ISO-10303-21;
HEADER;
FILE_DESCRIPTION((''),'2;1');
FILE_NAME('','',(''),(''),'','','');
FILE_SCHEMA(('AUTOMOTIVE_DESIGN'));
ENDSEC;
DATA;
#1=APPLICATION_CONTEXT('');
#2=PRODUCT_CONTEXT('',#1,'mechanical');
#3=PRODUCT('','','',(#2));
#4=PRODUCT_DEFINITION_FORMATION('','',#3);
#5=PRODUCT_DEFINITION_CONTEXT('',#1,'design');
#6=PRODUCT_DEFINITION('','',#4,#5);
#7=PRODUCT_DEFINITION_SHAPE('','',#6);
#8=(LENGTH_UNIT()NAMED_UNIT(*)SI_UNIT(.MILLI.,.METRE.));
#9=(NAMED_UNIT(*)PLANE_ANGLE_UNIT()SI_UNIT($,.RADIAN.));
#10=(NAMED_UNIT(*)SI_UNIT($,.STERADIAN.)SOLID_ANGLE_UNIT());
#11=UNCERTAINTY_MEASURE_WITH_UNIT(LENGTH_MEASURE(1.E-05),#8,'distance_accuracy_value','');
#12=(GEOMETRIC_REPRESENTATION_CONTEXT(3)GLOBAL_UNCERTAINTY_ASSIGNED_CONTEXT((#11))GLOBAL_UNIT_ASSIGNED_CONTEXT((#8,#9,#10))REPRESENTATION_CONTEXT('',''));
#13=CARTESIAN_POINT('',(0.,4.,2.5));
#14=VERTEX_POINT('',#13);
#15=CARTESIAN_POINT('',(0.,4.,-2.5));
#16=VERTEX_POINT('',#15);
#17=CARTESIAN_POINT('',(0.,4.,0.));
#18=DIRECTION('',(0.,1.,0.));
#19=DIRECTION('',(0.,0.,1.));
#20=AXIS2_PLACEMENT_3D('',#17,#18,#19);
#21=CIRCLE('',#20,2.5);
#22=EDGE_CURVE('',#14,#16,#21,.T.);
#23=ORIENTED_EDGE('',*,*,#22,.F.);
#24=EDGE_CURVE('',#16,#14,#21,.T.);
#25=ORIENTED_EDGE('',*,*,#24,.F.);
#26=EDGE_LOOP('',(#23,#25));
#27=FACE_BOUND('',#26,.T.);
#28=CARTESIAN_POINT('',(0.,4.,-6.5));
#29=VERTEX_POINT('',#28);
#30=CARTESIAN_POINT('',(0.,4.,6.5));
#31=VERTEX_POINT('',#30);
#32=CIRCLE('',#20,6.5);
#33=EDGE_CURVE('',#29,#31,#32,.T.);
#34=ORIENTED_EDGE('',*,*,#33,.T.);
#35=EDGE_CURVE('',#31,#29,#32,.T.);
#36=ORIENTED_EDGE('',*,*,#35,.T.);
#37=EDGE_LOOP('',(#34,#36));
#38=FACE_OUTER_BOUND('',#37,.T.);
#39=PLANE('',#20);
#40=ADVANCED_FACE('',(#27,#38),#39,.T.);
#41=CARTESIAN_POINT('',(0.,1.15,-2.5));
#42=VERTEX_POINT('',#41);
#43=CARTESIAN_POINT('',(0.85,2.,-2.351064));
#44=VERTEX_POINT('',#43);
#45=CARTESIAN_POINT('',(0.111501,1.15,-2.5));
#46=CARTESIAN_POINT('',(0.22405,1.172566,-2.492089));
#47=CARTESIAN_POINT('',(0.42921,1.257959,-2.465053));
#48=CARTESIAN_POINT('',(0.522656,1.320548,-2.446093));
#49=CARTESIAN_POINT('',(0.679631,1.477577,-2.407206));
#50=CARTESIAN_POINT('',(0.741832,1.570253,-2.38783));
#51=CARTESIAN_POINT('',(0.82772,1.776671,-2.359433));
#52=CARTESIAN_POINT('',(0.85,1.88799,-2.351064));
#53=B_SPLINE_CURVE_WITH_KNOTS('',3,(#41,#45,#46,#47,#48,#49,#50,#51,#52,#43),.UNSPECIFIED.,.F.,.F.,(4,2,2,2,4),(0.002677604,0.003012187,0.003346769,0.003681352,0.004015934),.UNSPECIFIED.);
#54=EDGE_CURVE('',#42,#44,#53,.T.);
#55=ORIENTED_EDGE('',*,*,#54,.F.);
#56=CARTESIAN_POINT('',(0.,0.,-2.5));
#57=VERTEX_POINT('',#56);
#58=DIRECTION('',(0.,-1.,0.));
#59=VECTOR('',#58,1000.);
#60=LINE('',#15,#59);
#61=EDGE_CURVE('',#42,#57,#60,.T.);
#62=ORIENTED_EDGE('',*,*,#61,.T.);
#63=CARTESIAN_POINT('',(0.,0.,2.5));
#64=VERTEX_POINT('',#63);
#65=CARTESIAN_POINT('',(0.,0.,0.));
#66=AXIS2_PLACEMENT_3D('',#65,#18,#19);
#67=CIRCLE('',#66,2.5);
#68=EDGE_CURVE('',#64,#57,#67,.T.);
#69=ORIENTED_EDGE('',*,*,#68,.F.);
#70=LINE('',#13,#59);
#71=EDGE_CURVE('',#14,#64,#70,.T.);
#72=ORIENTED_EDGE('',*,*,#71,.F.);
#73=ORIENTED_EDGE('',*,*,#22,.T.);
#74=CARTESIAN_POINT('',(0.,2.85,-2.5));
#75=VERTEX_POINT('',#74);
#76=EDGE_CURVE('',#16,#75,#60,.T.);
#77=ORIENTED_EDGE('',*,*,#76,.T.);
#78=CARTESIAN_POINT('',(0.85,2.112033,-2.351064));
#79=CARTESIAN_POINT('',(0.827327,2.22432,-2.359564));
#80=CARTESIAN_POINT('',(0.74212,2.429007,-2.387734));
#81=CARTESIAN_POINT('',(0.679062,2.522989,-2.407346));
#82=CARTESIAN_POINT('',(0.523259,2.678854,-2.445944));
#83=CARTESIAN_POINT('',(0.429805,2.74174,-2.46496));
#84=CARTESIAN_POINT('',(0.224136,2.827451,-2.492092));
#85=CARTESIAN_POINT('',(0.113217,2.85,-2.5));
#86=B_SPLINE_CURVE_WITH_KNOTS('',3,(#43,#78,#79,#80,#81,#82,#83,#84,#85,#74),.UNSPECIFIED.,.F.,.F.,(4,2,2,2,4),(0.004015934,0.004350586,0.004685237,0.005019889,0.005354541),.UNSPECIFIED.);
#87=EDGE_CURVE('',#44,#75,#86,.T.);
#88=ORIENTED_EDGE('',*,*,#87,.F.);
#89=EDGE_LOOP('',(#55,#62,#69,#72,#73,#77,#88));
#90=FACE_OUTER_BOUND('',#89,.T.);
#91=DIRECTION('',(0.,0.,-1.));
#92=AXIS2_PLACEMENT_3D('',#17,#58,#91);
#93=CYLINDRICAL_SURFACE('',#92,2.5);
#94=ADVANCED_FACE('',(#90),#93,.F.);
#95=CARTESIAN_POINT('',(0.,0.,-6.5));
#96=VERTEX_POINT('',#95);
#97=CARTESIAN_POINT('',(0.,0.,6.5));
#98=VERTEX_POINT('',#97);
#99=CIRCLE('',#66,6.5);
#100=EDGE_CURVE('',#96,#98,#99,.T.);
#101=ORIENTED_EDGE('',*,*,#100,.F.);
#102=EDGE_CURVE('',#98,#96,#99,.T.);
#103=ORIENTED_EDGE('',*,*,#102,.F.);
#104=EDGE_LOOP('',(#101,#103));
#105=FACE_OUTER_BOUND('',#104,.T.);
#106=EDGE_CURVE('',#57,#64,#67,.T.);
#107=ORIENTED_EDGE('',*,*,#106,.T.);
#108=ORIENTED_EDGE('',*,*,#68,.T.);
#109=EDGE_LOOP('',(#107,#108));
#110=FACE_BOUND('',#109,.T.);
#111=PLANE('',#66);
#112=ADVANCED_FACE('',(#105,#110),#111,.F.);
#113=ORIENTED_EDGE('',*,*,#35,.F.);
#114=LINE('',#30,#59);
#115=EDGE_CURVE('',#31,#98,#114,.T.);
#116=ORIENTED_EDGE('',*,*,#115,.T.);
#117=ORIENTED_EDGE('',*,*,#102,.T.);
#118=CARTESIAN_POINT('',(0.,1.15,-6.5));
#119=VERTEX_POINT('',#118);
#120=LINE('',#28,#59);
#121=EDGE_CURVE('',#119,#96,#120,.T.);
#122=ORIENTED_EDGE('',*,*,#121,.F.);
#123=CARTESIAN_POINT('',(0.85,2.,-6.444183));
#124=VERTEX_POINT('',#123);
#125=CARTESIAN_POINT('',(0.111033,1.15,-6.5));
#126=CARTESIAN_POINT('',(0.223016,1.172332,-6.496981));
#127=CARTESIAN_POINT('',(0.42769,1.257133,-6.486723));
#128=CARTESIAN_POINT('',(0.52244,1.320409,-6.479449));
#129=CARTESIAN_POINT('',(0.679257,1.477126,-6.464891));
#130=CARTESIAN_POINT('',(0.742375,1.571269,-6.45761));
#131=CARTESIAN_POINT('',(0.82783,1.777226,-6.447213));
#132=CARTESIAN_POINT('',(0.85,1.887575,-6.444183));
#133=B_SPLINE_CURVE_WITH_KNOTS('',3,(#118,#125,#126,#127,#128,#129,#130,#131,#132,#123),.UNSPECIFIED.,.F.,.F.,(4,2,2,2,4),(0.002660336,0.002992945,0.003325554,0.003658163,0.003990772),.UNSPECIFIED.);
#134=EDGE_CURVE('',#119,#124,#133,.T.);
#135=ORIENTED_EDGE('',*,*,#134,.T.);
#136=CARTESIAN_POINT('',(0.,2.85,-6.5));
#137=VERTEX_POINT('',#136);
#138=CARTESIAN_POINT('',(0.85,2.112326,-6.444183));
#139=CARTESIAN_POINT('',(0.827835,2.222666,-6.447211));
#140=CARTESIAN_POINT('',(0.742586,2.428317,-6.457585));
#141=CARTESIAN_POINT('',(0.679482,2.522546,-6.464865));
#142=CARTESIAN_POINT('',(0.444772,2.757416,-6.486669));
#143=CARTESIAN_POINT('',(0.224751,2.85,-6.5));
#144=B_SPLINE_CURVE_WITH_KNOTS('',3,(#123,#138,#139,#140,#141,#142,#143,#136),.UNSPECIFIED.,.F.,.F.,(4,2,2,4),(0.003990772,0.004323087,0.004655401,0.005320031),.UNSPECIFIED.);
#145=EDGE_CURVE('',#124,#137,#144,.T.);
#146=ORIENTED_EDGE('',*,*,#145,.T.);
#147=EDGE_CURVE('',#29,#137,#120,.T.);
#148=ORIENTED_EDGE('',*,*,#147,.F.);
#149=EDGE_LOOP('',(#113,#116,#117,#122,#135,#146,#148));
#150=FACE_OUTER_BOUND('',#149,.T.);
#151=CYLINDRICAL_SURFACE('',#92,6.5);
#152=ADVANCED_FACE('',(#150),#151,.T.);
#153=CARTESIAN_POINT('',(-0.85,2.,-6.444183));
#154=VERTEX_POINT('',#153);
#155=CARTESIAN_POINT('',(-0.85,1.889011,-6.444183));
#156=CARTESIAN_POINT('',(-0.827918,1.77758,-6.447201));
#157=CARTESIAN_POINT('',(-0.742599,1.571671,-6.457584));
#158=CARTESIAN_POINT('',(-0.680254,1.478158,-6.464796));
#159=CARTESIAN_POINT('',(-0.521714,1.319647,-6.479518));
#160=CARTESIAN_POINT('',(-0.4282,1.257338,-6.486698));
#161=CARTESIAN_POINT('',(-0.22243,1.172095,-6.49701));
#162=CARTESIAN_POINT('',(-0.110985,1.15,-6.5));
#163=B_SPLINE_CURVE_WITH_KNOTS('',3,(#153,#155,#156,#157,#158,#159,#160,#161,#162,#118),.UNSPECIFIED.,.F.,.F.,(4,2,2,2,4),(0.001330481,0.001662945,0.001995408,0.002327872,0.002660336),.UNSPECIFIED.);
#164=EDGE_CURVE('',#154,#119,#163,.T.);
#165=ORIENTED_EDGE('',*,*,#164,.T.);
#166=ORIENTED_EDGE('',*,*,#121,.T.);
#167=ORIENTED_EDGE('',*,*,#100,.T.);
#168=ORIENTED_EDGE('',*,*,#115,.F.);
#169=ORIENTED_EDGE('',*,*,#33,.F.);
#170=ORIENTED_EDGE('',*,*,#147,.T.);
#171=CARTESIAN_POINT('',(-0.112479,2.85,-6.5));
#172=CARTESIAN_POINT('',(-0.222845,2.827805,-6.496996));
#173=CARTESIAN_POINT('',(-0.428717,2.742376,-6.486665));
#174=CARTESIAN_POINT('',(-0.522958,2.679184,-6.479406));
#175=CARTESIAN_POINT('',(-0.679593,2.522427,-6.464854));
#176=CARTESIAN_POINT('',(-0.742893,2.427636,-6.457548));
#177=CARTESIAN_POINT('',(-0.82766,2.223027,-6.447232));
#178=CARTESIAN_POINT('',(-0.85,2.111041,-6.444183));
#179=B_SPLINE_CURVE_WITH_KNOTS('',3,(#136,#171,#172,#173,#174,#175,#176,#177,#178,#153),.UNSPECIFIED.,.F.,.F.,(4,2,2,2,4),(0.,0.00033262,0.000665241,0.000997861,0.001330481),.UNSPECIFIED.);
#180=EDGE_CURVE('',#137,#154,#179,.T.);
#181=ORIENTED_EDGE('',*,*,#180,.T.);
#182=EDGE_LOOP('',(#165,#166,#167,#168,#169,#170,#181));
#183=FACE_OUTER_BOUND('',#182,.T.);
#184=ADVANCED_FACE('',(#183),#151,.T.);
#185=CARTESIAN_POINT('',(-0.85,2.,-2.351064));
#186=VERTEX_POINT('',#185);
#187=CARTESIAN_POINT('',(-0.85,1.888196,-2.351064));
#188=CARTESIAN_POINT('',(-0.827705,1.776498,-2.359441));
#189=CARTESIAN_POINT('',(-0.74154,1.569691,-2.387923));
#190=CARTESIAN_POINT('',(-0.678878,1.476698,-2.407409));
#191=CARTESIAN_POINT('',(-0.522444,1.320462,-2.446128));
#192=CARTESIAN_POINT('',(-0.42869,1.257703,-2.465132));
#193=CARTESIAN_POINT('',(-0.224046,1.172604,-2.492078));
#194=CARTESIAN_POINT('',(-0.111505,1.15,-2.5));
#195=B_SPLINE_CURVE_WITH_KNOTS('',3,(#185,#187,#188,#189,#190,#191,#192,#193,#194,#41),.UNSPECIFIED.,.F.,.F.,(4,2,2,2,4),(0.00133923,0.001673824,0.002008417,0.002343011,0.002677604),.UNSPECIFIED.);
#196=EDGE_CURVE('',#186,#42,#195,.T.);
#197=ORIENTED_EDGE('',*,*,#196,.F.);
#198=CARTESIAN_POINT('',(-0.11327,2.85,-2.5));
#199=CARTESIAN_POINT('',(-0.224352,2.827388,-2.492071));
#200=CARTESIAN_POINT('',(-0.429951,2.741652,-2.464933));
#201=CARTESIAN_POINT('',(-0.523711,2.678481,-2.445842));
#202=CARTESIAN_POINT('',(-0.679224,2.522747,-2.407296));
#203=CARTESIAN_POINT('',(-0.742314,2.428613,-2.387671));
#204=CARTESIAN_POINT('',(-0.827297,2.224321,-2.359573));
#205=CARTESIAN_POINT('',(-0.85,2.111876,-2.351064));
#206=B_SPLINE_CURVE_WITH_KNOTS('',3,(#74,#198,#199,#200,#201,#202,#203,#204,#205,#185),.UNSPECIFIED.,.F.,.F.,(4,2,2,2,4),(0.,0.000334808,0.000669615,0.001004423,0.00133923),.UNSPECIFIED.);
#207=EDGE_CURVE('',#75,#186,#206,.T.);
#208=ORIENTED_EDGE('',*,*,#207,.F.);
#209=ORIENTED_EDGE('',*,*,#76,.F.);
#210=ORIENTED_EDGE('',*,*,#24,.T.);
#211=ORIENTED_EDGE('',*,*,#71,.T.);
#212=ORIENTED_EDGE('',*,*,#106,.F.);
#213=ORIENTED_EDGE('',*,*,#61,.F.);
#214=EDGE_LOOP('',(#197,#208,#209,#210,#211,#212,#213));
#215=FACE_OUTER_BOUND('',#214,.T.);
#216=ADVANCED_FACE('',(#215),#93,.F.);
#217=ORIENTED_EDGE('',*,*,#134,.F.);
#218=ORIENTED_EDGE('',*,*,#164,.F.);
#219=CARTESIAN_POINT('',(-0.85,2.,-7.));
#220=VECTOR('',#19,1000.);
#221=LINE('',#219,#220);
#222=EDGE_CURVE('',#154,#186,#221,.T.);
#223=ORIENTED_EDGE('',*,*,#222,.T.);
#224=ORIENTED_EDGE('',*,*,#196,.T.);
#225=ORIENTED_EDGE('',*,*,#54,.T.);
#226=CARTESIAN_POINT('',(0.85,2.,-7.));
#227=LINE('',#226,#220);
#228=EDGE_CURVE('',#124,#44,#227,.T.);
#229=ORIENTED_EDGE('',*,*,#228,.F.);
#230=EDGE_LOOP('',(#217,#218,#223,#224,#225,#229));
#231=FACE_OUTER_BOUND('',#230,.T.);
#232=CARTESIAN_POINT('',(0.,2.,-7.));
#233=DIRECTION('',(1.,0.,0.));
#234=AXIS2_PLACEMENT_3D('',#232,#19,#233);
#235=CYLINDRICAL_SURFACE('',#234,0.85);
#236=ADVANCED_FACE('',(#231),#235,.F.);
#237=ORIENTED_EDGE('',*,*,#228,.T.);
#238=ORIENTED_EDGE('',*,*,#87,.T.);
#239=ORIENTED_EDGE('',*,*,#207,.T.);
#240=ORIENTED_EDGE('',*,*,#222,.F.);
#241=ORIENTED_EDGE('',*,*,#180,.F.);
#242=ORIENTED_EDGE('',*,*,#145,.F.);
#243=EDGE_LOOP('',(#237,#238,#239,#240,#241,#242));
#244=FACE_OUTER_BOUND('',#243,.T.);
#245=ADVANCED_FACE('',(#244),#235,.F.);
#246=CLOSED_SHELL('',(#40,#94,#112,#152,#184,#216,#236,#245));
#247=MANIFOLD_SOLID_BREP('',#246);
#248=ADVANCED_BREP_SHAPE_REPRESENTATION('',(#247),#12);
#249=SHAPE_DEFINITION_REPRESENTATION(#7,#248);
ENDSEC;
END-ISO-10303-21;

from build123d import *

# Parameters (mm, degrees)
RING_PROFILE_13_X_5_R   = 6.5
RING_PROFILE_13_X_5_R_2 = 2.5
COVER_RING_DEPTH        = 4
RADIAL_HOLE_PROFILE_2_R = 0.85
RADIAL_HOLE_2_DEPTH     = 7


with BuildPart() as part:
    # Ring Profile Ø13 x Ø5 → Cover Ring (new body)
    with BuildSketch(Plane(origin=(0, 0, 0), x_dir=(1, 0, 0), z_dir=(0, 1, 0))):
        with Locations(Location((0, 0, 0), (0, 0, 270))):
            Circle(RING_PROFILE_13_X_5_R)
        with Locations(Location((0, 0, 0), (0, 0, 270))):
            Circle(RING_PROFILE_13_X_5_R_2, mode=Mode.SUBTRACT)
    extrude(amount=COVER_RING_DEPTH)

    # Radial Hole Profile Ø2 → Radial Hole Ø2 (cut)
    with BuildSketch(Plane.XY):
        with Locations(Location((0, 2, 0), (0, 0, 90))):
            Circle(RADIAL_HOLE_PROFILE_2_R)
    extrude(amount=-RADIAL_HOLE_2_DEPTH, mode=Mode.SUBTRACT)


solid = part.part
